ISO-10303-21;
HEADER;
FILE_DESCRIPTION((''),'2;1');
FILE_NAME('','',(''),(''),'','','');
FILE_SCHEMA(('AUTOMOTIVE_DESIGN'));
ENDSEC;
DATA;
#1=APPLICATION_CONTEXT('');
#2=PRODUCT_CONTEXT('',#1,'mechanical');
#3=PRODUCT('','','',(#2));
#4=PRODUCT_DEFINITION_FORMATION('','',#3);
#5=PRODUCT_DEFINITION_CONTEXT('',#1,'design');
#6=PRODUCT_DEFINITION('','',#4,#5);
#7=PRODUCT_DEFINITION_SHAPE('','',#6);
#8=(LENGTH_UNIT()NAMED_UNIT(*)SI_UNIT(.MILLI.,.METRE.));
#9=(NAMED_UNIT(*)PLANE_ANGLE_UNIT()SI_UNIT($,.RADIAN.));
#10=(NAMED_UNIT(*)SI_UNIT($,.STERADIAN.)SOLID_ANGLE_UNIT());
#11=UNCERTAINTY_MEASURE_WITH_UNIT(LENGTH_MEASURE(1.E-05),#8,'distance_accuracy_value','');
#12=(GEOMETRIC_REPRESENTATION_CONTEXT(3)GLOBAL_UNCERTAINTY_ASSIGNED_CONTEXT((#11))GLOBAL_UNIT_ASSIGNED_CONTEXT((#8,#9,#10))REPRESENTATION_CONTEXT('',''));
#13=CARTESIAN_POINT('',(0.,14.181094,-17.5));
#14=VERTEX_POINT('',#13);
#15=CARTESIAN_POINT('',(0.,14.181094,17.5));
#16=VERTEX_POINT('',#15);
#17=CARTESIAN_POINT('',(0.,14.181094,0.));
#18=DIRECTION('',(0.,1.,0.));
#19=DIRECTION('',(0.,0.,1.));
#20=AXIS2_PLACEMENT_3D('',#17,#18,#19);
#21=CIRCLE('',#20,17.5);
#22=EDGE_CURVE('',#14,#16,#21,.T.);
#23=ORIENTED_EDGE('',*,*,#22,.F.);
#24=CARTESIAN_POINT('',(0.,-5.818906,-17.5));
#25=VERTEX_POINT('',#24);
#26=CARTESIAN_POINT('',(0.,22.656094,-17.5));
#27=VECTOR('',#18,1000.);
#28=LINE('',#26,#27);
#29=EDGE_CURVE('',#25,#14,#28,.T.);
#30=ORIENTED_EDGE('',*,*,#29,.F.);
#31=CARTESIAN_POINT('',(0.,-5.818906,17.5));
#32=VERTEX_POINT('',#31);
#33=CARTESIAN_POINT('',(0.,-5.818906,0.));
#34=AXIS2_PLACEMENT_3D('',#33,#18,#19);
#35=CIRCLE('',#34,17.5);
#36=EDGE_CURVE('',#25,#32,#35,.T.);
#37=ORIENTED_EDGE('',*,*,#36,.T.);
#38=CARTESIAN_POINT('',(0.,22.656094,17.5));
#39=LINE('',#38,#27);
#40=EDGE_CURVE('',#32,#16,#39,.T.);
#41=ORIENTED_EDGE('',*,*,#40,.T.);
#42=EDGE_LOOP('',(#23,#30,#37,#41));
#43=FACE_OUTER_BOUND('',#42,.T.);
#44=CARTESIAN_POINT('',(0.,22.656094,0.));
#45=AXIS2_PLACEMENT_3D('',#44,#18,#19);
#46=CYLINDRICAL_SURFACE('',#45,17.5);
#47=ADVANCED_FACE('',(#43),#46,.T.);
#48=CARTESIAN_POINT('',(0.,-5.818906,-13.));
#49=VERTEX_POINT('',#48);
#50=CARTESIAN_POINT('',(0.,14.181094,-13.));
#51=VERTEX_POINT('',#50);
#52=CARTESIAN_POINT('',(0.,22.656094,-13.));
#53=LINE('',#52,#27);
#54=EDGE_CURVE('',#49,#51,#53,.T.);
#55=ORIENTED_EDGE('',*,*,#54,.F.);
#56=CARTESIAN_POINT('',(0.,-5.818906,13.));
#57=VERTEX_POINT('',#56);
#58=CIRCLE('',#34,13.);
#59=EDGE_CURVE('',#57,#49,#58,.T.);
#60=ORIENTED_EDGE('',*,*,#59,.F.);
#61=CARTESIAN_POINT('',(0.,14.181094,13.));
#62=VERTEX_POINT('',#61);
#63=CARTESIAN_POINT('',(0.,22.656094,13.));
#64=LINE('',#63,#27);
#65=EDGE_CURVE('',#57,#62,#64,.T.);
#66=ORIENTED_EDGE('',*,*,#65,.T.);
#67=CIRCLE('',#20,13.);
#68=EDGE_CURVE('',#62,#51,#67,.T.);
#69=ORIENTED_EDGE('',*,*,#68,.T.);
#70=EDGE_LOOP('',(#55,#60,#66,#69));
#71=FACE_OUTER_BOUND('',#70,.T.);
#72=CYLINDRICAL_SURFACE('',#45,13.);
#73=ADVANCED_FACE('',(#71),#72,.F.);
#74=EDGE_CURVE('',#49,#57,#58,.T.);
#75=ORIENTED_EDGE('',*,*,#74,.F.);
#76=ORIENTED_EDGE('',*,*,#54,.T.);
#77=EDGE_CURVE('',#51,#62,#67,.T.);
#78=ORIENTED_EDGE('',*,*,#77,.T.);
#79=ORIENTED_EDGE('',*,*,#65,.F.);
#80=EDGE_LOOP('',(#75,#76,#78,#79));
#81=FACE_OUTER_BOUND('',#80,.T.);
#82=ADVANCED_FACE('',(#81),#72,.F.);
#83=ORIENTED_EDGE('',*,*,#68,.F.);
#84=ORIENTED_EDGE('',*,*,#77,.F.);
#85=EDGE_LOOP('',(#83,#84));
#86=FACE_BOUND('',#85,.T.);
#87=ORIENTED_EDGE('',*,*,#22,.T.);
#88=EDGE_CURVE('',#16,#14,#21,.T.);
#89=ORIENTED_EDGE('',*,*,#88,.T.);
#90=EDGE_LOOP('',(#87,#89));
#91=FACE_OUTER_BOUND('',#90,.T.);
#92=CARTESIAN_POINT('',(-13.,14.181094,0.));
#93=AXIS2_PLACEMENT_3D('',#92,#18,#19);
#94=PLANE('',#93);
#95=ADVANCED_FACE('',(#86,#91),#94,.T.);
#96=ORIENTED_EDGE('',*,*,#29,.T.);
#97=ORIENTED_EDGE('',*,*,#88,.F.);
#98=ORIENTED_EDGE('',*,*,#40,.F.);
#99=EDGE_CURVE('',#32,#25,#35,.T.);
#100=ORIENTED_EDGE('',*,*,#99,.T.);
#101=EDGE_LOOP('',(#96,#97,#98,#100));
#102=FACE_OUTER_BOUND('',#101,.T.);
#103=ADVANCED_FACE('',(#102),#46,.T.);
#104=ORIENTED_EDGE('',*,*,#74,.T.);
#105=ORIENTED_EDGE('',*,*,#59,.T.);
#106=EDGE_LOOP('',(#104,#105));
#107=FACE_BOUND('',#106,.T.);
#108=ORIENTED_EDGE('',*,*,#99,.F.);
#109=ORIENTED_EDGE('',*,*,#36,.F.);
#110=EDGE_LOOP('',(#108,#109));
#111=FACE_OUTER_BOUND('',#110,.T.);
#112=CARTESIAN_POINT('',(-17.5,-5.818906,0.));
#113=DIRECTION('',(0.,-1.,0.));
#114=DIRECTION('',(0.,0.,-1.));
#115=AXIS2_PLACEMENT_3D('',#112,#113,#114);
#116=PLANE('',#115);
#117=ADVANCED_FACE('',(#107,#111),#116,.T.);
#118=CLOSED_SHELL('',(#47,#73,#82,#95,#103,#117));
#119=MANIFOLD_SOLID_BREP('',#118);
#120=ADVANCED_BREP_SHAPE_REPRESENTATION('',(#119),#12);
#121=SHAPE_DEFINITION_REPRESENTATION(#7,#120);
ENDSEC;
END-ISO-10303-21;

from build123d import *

# Parameters (mm, degrees)
SKETCH1_W = 4.5
SKETCH1_H = 20


with BuildPart() as part:
    # Sketch1 → Revolve1 (revolve)
    with BuildSketch(Plane.XY, mode=Mode.PRIVATE) as revolve1_sk:
        with Locations((-15.25, 4.181093582)):
            Rectangle(SKETCH1_W, SKETCH1_H)
    revolve(revolve1_sk.sketch.rotate(Axis((0, 22.656093582, 0), (0, -1, 0)), 270), axis=Axis((0, 22.656093582, 0), (0, -1, 0)))


solid = part.part
